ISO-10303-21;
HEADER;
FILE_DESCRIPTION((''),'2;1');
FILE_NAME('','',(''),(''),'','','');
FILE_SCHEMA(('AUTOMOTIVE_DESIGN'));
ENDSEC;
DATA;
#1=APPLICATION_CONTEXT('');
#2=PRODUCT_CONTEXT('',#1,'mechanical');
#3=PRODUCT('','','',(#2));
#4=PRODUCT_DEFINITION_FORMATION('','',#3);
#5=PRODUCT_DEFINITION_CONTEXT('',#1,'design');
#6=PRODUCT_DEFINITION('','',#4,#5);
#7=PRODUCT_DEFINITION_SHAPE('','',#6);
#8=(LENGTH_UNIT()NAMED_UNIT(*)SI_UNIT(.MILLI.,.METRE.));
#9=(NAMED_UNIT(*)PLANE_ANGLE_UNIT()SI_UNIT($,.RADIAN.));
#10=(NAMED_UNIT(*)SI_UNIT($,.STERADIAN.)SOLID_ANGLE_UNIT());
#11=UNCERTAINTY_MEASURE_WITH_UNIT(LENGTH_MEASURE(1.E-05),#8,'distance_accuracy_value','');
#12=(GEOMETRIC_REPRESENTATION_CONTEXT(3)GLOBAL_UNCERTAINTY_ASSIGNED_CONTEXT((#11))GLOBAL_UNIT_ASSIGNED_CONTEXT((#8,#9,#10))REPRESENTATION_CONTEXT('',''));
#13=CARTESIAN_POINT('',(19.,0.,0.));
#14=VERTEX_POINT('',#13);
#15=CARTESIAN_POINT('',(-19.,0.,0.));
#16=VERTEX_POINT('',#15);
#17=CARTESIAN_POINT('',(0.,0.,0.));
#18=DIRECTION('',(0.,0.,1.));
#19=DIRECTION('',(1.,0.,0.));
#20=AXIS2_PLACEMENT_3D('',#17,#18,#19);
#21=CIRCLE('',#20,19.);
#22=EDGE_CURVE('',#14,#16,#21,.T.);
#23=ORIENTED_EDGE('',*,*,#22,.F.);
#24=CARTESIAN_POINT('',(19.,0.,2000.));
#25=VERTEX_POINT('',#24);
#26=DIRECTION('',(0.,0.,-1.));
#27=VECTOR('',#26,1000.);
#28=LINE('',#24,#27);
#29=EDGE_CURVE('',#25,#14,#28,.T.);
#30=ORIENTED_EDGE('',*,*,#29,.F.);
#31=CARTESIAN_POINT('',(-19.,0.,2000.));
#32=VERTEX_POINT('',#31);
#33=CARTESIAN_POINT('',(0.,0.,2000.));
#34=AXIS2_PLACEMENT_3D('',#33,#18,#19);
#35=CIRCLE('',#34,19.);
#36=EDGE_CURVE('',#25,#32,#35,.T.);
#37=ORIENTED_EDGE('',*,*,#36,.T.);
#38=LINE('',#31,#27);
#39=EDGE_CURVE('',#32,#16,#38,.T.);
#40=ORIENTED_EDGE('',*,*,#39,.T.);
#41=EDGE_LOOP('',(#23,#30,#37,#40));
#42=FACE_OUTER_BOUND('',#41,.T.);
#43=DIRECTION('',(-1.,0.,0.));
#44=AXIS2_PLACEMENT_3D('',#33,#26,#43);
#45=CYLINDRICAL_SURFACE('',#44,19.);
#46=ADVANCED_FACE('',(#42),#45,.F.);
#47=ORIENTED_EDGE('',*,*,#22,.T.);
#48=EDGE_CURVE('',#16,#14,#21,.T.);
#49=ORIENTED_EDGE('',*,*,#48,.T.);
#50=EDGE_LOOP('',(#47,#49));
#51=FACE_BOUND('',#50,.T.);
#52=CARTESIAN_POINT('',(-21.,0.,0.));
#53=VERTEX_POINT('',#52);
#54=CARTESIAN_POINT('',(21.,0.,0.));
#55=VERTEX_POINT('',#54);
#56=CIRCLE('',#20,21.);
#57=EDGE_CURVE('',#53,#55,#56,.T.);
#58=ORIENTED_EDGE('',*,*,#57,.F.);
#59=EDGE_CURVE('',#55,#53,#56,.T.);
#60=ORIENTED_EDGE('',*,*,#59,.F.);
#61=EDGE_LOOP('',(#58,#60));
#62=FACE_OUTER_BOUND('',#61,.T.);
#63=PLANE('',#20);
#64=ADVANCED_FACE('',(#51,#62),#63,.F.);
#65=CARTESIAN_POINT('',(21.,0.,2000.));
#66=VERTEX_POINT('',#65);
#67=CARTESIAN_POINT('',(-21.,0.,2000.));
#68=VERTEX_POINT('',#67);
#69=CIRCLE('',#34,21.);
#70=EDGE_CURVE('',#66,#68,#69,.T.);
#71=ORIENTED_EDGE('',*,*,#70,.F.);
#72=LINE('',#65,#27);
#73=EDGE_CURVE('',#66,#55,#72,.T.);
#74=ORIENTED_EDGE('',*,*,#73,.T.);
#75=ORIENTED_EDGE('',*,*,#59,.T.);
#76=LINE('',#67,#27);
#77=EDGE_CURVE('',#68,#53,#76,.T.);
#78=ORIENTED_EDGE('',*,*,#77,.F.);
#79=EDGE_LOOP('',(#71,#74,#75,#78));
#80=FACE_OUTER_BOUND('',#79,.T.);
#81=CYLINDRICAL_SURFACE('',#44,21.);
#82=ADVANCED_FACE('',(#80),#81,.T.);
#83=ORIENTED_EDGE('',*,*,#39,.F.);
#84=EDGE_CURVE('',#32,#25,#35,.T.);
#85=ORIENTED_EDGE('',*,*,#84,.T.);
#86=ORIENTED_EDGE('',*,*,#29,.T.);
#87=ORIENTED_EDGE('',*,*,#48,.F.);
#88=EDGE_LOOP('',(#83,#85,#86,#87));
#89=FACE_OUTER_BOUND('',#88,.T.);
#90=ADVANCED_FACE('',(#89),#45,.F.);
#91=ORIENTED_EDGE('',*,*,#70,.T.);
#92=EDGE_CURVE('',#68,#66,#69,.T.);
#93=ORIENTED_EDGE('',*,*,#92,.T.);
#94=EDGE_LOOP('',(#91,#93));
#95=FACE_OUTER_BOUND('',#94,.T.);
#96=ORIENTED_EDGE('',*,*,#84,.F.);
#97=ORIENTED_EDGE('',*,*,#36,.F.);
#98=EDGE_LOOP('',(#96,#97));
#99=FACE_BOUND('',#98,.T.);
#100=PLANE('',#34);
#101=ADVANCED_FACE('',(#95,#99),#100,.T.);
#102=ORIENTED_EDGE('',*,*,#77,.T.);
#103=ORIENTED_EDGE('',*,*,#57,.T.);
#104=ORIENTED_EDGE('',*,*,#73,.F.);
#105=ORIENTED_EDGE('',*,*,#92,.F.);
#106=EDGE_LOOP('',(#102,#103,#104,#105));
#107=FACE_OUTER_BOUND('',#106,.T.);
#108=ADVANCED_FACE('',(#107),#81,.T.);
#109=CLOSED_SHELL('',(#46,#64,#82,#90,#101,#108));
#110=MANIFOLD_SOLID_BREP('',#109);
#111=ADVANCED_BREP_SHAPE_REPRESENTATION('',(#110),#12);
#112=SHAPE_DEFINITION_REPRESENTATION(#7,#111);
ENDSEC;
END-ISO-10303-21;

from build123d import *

# Parameters (mm, degrees)
SKETCH1_R           = 21
SKETCH1_R_2         = 19
BOSS_EXTRUDE1_DEPTH = 2000


with BuildPart() as part:
    # Sketch1 → Boss-Extrude1 (new body)
    with BuildSketch(Plane.XY):
        Circle(SKETCH1_R)
        Circle(SKETCH1_R_2, mode=Mode.SUBTRACT)
    extrude(amount=BOSS_EXTRUDE1_DEPTH)


solid = part.part
